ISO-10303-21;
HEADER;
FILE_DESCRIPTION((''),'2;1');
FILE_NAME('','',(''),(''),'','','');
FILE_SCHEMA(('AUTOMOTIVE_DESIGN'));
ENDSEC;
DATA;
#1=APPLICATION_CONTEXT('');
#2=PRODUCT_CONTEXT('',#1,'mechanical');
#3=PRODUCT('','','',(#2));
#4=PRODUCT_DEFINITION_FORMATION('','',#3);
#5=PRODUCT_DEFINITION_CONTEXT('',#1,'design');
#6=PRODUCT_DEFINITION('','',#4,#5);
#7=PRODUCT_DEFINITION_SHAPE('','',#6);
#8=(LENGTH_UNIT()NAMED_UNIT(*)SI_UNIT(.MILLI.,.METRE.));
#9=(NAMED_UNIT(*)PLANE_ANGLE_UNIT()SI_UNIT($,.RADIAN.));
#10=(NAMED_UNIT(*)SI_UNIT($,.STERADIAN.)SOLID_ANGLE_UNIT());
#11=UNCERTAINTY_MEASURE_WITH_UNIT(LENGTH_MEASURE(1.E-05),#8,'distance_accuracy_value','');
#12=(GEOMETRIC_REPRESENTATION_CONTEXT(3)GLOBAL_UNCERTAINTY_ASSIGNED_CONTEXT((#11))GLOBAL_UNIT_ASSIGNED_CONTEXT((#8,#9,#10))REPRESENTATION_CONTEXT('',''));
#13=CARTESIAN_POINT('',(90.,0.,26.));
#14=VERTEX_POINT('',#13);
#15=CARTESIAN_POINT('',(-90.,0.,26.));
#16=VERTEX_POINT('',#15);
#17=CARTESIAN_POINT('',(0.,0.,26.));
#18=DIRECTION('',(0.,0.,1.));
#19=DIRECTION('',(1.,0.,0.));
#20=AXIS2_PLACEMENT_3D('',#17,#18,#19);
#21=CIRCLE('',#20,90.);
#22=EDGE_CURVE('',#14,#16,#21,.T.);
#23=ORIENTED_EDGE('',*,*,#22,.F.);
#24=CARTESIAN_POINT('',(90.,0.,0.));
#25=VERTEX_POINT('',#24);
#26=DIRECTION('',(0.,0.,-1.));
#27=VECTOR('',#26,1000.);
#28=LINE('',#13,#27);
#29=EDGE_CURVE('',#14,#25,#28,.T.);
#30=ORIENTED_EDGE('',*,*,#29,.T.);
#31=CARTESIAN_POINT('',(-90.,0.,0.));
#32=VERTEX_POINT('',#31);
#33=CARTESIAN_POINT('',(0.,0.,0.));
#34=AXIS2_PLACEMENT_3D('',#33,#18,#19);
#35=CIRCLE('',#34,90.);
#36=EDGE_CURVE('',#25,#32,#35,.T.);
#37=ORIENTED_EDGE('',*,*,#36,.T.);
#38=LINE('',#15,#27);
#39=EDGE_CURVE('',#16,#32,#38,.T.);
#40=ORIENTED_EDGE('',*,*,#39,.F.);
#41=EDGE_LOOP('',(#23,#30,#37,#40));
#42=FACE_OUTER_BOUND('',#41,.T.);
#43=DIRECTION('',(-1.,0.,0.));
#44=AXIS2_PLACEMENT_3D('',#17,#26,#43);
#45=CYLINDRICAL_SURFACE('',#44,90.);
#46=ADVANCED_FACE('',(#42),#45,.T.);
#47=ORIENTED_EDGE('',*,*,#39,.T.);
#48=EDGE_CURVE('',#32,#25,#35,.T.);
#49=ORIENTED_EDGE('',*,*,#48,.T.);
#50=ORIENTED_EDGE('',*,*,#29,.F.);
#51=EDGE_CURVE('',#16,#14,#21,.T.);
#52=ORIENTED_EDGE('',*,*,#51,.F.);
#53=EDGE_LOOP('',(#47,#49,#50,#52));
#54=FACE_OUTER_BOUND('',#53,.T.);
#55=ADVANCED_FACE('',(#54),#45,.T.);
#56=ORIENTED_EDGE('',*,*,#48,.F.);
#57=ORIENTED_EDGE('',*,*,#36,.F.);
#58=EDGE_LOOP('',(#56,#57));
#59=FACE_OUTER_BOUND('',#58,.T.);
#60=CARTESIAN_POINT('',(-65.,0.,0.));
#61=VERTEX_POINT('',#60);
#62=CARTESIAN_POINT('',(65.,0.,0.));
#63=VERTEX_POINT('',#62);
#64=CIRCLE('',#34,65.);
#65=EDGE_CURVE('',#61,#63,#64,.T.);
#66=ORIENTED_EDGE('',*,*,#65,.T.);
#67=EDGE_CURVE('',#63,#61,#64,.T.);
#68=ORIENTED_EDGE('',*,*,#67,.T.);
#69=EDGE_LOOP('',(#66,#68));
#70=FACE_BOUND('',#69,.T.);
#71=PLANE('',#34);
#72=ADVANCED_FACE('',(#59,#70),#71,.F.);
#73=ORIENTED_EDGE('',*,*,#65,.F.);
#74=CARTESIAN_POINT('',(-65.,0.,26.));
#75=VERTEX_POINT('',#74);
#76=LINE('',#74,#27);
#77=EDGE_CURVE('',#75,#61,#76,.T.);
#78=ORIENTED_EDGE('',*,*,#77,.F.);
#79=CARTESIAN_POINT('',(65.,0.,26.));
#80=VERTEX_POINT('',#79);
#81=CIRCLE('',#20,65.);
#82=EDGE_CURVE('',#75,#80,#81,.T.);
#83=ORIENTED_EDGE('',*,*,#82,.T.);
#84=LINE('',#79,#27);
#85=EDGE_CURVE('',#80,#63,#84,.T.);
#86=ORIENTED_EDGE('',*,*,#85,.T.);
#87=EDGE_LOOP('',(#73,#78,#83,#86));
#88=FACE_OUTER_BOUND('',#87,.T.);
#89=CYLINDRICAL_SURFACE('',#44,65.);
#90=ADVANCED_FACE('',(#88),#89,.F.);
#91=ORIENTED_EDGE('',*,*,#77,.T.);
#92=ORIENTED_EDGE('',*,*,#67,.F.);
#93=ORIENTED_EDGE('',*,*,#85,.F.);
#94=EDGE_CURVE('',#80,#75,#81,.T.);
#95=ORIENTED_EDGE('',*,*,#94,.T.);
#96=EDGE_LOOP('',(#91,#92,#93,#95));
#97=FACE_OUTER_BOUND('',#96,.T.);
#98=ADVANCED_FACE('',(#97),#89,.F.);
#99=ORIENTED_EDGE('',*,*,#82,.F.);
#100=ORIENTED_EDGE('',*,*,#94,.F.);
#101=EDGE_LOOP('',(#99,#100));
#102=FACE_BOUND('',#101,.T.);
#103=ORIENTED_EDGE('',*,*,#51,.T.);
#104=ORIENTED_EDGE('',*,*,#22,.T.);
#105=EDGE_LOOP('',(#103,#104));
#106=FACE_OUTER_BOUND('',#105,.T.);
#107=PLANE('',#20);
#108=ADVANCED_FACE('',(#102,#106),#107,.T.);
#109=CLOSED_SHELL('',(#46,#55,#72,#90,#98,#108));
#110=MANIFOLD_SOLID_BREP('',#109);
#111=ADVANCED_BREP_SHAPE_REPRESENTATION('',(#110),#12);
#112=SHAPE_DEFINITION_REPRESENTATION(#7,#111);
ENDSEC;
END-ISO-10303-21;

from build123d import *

# Parameters (mm, degrees)
SKETCH1_R           = 90
SKETCH1_R_2         = 65
BOSS_EXTRUDE1_DEPTH = 26


with BuildPart() as part:
    # Sketch1 → Boss-Extrude1 (new body)
    with BuildSketch(Plane.XY):
        with Locations(Location((0, 0, 0), (0, 0, 180))):
            Circle(SKETCH1_R)
        with Locations(Location((0, 0, 0), (0, 0, 180))):
            Circle(SKETCH1_R_2, mode=Mode.SUBTRACT)
    extrude(amount=BOSS_EXTRUDE1_DEPTH)


solid = part.part
